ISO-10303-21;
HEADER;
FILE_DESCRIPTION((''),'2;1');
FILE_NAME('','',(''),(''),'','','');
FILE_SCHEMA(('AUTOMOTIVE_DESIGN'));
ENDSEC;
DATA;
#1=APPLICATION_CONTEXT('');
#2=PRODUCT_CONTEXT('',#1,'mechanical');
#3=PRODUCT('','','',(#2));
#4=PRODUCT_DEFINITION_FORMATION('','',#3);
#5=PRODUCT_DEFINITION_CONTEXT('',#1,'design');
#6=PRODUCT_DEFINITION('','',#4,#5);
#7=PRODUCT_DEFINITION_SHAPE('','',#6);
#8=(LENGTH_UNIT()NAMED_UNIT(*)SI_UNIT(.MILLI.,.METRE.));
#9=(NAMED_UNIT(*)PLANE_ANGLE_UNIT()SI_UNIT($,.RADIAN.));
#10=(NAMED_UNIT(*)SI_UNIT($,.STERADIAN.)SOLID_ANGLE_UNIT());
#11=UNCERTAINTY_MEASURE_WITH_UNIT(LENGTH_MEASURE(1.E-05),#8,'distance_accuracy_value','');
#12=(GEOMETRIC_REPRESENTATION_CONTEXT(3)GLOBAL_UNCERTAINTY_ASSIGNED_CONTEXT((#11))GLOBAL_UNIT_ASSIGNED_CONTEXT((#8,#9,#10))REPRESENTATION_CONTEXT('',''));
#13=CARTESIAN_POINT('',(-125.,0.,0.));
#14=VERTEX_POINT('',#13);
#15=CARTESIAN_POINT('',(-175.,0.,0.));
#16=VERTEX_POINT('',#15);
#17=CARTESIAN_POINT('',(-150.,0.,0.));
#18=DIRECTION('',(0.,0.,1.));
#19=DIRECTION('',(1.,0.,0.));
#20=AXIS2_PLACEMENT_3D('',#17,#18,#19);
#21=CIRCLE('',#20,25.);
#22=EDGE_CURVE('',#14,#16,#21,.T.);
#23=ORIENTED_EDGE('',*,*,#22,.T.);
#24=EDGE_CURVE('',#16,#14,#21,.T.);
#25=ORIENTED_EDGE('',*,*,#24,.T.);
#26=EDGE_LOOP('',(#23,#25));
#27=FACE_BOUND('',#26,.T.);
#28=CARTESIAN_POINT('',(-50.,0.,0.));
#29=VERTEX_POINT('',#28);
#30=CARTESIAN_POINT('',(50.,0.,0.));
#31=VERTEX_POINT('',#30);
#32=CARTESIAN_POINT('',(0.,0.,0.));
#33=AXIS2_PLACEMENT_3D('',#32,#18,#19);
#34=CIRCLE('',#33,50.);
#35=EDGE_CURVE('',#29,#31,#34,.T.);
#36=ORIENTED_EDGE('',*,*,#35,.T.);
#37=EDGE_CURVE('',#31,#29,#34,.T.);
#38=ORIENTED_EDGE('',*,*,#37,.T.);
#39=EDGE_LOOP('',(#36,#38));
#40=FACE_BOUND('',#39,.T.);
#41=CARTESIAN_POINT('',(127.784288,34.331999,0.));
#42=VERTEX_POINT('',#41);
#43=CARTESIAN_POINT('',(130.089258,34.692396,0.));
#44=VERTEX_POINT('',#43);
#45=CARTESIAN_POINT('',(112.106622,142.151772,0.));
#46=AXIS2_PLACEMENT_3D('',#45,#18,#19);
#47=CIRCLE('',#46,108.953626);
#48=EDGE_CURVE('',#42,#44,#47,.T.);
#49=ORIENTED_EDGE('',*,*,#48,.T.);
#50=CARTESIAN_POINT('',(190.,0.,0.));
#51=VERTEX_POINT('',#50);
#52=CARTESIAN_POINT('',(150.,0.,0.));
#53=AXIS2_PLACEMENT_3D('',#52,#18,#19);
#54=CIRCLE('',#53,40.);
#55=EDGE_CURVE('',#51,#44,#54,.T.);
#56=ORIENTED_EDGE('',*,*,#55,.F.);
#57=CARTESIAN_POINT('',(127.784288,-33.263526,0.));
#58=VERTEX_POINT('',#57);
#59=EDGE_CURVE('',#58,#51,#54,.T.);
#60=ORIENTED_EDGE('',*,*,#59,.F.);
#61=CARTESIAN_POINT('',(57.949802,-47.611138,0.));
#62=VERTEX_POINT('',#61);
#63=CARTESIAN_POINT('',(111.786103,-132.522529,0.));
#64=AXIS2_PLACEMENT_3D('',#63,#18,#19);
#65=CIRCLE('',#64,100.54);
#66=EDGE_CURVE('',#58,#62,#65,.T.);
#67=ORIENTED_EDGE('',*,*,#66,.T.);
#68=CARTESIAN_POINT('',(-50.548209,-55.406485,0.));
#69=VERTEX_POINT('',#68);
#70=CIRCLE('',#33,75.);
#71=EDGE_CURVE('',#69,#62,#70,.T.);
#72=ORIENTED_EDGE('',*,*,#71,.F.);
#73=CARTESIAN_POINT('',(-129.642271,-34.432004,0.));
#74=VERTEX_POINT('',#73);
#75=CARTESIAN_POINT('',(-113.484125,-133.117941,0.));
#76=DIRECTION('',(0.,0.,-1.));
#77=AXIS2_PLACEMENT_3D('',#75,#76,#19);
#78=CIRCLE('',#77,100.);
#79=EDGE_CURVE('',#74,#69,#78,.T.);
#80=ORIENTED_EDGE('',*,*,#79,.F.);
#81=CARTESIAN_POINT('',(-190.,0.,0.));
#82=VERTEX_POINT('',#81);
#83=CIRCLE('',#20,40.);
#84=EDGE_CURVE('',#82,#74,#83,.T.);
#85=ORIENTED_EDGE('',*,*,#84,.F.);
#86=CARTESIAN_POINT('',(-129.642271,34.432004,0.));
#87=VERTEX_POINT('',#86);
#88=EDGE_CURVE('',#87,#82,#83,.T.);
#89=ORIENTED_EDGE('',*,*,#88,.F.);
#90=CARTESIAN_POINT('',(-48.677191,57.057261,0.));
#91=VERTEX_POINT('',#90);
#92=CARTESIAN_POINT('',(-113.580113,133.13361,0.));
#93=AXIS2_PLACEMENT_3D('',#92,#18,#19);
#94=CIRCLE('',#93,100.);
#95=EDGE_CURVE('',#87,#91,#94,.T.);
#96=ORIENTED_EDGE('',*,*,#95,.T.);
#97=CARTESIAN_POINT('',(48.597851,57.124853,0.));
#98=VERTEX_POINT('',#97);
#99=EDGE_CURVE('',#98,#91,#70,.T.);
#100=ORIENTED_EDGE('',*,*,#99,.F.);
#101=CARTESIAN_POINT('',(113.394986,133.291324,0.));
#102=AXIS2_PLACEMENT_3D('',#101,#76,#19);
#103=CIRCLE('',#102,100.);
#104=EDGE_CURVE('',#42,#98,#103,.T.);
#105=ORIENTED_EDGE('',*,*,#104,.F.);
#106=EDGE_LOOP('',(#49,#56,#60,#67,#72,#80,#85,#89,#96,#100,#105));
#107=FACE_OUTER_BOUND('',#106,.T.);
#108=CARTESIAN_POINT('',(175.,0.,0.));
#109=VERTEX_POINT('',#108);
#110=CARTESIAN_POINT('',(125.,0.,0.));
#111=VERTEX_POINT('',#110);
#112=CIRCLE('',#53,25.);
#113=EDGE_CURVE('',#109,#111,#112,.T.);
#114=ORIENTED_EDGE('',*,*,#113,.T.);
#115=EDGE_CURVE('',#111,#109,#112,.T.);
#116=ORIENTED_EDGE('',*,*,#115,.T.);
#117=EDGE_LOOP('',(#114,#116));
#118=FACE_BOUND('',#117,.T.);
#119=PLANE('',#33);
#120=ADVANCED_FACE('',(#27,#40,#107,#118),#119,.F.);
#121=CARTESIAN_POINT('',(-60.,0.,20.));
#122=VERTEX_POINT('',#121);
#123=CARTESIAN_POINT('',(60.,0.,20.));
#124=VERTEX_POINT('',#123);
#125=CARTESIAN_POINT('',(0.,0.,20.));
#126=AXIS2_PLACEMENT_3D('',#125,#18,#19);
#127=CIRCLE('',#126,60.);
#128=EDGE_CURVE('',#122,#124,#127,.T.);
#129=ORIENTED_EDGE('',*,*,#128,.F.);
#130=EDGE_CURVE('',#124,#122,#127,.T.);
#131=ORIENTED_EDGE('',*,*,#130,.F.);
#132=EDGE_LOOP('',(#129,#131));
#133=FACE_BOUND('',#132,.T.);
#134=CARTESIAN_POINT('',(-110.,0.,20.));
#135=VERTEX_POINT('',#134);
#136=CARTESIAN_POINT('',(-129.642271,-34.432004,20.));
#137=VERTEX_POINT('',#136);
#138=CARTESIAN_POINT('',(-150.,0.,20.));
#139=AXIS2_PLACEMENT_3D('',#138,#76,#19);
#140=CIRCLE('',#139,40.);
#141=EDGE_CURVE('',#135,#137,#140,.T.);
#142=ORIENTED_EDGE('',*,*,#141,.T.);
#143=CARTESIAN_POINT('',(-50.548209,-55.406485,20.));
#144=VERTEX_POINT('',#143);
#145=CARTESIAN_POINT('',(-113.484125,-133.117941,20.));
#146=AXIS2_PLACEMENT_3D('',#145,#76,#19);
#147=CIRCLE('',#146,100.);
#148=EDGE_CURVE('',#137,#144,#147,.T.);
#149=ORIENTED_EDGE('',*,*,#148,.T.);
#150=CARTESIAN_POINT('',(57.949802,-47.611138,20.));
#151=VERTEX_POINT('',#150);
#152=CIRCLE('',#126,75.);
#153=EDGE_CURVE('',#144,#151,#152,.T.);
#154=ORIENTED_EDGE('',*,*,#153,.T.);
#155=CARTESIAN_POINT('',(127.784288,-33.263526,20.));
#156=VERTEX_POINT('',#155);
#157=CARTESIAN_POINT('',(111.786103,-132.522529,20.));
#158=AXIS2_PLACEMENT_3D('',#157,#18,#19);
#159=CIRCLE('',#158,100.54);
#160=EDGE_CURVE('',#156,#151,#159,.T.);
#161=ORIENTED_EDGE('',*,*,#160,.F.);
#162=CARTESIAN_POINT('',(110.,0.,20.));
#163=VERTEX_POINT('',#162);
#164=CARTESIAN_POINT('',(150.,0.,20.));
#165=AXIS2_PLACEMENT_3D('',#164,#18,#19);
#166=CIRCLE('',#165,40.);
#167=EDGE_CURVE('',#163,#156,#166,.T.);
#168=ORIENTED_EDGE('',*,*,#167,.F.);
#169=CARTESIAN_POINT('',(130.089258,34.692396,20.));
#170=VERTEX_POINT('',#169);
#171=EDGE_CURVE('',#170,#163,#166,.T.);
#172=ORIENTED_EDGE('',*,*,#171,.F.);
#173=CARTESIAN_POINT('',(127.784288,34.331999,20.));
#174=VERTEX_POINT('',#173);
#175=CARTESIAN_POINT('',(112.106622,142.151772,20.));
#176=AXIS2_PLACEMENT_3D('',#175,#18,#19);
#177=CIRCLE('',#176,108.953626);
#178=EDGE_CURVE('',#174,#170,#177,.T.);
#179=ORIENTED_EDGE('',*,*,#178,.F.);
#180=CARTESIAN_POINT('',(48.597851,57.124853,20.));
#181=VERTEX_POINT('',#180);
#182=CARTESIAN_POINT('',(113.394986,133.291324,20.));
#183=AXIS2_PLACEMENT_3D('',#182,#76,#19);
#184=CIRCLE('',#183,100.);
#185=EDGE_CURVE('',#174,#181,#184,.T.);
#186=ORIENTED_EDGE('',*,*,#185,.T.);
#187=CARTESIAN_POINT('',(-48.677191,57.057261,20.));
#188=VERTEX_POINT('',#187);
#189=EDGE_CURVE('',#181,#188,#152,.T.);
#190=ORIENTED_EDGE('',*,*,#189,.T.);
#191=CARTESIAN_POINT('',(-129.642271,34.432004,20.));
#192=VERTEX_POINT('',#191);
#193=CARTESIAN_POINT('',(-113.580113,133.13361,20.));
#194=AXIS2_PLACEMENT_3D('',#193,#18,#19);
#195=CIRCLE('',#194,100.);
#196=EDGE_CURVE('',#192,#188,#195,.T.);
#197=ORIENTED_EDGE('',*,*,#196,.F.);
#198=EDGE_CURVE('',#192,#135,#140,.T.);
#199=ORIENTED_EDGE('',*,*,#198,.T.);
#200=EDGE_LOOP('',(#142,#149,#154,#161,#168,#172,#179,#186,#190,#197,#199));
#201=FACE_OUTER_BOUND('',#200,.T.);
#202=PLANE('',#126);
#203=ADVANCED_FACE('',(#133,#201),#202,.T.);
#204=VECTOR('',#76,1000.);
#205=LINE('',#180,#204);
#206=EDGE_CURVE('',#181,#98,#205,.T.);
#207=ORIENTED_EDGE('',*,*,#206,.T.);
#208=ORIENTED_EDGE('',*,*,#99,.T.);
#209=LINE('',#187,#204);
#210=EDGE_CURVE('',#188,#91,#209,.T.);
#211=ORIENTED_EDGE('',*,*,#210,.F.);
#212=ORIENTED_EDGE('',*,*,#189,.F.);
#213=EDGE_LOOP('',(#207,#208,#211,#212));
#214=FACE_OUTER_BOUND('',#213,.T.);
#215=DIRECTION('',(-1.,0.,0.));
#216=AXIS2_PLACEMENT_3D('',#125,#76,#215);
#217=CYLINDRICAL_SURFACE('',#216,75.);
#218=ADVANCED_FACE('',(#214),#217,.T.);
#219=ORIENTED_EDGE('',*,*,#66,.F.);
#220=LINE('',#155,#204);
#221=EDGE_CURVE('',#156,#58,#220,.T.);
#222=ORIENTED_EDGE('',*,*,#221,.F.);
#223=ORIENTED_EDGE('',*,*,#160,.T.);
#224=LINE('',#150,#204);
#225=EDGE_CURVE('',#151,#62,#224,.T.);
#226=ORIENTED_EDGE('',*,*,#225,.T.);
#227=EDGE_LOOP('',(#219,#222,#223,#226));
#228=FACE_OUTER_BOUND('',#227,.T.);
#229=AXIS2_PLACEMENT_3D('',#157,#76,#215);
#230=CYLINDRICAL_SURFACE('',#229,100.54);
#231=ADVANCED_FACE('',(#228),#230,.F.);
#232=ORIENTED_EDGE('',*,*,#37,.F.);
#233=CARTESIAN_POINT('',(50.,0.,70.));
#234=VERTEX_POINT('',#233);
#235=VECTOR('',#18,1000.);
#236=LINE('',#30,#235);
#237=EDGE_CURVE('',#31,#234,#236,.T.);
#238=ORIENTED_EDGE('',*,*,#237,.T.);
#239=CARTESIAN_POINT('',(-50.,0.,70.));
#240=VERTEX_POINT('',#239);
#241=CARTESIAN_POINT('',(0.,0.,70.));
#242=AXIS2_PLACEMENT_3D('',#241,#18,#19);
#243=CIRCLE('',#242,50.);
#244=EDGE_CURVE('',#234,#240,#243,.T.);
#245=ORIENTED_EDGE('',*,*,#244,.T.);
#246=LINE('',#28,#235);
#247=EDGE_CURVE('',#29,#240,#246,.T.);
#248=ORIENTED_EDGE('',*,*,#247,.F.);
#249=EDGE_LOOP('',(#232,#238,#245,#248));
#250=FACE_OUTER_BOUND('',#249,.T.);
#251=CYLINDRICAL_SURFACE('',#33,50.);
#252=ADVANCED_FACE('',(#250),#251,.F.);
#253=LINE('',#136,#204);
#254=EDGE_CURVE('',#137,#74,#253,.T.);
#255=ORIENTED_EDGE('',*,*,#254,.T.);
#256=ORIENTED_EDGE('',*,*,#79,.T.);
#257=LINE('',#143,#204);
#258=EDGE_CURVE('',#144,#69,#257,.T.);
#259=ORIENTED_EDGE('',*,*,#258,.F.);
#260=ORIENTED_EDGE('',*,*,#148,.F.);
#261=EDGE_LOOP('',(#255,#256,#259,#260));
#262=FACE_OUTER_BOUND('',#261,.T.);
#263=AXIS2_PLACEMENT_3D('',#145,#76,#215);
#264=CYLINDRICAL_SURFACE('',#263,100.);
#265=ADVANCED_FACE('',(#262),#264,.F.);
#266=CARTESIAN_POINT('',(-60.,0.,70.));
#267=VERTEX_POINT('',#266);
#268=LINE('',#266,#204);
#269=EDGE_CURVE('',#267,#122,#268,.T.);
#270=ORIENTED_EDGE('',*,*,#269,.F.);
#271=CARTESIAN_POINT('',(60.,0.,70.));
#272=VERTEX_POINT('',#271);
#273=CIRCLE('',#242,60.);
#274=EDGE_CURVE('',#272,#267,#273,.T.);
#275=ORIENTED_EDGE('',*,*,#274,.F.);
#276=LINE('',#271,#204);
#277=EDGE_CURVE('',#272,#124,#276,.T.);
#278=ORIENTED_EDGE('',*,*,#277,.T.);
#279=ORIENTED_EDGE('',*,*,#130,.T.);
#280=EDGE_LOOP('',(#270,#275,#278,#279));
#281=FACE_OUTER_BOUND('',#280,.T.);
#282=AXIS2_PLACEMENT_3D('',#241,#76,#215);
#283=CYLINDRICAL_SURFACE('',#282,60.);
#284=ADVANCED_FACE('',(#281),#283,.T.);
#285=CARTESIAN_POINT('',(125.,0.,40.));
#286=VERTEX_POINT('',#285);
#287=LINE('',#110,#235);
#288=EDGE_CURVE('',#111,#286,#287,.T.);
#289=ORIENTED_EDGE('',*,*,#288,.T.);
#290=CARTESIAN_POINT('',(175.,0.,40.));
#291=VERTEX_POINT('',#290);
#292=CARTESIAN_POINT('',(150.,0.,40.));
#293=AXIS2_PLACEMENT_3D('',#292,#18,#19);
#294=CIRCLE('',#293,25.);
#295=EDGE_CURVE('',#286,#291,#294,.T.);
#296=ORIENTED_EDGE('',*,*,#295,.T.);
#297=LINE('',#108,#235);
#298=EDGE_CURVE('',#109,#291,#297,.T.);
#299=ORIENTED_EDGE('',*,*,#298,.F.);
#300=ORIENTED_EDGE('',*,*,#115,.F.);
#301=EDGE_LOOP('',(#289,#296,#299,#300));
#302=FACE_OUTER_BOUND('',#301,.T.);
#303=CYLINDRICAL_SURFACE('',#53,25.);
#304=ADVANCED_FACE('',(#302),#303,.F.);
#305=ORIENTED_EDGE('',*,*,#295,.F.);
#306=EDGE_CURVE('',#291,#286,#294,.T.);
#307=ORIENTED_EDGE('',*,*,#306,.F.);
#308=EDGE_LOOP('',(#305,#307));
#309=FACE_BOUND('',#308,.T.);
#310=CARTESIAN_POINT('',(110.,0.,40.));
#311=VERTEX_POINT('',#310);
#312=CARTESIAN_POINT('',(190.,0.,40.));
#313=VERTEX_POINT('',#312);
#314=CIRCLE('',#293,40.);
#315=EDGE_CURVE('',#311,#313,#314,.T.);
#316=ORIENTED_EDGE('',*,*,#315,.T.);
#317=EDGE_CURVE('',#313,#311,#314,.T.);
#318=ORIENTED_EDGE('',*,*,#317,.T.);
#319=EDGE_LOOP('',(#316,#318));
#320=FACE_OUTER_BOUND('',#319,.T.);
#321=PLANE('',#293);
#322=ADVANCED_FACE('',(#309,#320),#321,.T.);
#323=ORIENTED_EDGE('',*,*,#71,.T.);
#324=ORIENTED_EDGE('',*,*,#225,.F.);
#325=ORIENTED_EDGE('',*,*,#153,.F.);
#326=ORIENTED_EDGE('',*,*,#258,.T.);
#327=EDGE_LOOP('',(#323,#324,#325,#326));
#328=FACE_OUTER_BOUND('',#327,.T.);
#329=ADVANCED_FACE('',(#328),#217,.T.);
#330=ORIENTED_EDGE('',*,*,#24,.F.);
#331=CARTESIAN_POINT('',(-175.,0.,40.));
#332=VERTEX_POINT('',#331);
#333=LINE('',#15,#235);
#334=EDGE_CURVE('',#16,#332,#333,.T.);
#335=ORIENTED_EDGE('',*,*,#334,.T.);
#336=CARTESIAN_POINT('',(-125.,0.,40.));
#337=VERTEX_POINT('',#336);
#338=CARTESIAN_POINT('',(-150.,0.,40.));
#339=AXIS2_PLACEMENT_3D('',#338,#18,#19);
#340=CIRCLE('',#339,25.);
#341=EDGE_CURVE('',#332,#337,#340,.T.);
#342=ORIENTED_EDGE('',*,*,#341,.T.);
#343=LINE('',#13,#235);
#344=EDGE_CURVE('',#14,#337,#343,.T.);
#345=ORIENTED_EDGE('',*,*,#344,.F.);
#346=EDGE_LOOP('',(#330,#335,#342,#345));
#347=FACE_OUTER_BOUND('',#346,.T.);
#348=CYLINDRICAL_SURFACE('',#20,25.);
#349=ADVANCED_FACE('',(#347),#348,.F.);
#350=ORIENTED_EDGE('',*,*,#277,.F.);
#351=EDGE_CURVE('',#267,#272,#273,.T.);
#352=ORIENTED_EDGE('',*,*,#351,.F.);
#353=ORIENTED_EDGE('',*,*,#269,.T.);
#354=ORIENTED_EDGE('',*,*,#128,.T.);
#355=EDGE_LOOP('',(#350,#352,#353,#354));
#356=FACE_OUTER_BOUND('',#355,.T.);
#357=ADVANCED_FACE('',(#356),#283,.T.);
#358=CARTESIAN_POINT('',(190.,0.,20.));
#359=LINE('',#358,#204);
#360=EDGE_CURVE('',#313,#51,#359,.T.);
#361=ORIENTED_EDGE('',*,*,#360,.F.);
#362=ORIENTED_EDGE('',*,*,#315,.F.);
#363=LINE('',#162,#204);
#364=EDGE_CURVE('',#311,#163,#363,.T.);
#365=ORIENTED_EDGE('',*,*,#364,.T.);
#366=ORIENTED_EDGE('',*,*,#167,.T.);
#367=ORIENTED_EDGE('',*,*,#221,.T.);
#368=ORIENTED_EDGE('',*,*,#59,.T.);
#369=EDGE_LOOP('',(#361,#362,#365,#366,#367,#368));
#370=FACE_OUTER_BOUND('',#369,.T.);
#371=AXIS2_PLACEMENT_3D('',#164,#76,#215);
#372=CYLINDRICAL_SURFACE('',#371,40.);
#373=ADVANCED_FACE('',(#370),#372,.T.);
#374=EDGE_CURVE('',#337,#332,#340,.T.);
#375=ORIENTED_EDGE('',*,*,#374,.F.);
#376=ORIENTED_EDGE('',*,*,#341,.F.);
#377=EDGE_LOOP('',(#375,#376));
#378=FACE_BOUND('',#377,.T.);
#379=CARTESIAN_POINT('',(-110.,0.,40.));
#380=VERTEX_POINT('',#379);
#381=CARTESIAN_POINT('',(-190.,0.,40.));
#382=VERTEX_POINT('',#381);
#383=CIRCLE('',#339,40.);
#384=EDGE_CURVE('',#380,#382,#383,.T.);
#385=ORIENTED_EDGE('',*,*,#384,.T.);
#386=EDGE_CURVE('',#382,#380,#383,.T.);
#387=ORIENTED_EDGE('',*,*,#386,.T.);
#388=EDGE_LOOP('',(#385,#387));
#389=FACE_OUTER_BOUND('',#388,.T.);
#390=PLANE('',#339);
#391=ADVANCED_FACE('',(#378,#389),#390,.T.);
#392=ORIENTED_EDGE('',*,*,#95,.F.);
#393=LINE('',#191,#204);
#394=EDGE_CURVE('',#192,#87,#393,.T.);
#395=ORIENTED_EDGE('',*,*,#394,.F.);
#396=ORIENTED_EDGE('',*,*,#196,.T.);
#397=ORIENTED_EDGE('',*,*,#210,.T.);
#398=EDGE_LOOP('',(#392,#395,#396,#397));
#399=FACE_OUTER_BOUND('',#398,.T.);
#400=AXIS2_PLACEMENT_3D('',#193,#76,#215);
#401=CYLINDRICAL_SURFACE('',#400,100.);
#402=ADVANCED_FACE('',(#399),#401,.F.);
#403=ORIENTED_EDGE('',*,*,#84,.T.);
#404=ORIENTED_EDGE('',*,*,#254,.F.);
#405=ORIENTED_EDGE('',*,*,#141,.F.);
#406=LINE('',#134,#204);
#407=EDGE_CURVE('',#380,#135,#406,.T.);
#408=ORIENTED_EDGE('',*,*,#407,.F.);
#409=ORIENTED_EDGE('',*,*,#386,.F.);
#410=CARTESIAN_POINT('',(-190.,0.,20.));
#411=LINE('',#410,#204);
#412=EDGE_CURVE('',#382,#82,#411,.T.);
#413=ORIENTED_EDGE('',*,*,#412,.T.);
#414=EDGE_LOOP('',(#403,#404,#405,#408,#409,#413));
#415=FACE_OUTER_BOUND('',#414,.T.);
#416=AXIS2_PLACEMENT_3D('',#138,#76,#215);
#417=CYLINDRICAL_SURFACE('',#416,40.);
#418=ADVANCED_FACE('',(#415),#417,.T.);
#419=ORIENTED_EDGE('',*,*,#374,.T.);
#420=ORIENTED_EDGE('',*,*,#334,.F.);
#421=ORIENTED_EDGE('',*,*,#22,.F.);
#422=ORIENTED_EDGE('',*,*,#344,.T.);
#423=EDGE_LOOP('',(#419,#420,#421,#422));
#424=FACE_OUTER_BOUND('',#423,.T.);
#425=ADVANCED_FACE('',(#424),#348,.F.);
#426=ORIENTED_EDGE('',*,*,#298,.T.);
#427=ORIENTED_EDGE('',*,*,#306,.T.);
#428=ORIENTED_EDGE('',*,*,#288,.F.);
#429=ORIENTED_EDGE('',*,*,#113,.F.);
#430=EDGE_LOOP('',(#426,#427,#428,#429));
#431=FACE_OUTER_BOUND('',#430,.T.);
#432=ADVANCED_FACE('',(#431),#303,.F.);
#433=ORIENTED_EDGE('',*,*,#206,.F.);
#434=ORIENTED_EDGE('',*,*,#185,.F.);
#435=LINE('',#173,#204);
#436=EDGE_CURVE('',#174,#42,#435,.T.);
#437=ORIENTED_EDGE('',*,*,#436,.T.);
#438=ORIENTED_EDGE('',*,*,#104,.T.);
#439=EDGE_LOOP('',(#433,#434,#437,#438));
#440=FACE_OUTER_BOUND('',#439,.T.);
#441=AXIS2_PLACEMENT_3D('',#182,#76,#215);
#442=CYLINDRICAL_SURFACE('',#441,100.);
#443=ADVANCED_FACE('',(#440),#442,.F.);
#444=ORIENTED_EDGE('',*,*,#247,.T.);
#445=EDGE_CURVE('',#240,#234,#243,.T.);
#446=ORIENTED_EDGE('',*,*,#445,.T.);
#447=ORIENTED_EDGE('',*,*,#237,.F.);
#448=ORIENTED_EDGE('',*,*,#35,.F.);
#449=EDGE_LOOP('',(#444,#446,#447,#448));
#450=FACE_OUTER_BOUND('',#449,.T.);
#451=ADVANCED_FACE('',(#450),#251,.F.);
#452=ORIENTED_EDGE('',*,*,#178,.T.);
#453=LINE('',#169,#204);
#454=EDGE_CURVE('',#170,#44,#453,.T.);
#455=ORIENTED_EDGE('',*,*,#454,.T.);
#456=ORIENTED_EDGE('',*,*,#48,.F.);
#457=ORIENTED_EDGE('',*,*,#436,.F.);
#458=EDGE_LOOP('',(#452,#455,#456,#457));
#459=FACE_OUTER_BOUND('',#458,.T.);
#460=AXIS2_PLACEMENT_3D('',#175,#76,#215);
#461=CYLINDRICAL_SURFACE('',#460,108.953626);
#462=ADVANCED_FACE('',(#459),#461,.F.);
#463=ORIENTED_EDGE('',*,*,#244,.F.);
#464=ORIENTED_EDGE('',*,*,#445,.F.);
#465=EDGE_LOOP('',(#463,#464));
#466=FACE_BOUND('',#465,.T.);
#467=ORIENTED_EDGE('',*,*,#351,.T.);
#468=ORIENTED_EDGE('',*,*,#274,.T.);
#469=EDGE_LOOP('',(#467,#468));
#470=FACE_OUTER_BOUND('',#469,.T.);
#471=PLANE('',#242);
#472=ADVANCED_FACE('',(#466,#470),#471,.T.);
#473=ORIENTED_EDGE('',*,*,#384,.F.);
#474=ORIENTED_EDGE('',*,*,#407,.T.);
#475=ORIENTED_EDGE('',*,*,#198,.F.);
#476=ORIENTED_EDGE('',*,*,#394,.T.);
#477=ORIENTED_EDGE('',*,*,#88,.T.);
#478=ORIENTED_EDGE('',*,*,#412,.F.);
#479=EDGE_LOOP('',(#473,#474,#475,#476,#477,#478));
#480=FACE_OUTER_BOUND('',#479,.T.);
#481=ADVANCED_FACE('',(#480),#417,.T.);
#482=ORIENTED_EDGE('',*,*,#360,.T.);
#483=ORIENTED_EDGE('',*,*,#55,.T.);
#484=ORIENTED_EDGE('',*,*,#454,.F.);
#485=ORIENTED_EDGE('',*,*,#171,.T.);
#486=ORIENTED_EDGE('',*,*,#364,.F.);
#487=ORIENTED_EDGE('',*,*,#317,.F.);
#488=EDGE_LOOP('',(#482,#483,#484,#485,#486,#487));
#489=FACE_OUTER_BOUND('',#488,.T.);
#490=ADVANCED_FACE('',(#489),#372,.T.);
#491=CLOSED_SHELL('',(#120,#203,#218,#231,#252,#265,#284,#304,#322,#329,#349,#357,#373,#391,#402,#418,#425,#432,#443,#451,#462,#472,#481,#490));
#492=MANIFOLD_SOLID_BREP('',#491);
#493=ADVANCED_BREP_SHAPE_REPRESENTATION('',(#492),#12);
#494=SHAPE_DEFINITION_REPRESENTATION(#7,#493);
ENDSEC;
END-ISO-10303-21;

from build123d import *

# Parameters (mm, degrees)
LINK_PLATE_DEPTH      = 20
CENTER_BOSS_SKETCH_R  = 60
CENTER_BOSS_120_DEPTH = 50
CENTER_BORE_SKETCH_R  = 50
CENTER_BORE_100_DEPTH = 70
END_BOSS_A_SKETCH_R   = 40
END_BOSS_A_80_DEPTH   = 20
END_BOSS_B_SKETCH_R   = 40
END_BOSS_B_80_DEPTH   = 20
END_BORES_SKETCH_R    = 25
END_BORES_2X_50_DEPTH = 40


with BuildPart() as part:
    # Link Profile Sketch → Link Plate (new body)
    with BuildSketch(Plane.XY):
        with BuildLine():
            ThreePointArc((-129.642270948, 34.432003541), (-190, 0), (-129.642270948, -34.432003541))
            ThreePointArc((-129.642270948, -34.432003541), (-87.851681721, -36.458860817), (-50.548209333, -55.406484578))
            ThreePointArc((-50.548209333, -55.406484578), (5.374732367, -74.807167116), (57.949801632, -47.611138306))
            ThreePointArc((57.949801632, -47.611138306), (91.552609541, -34.039548838), (127.784288058, -33.263525714))
            ThreePointArc((127.784288058, -33.263525714), (189.977010396, -1.355964531), (130.089258317, 34.692396366))
            ThreePointArc((130.089258317, 34.692396366), (128.937737844, 34.506028192), (127.784288058, 34.331999196))
            ThreePointArc((127.784288058, 34.331999196), (85.734256685, 37.193020101), (48.597851254, 57.124853204))
            ThreePointArc((48.597851254, 57.124853204), (-0.052113987, 74.999981894), (-48.677191075, 57.057261317))
            ThreePointArc((-48.677191075, 57.057261317), (-86.6667217, 36.823333055), (-129.642270948, 34.432003541))
        make_face()
    extrude(amount=LINK_PLATE_DEPTH)

    # Center Boss Sketch → Center Boss Ø120 (add)
    with BuildSketch(Plane.XY.offset(20)):
        Circle(CENTER_BOSS_SKETCH_R)
    extrude(amount=CENTER_BOSS_120_DEPTH)

    # Center Bore Sketch → Center Bore Ø100 (cut)
    with BuildSketch(Plane.XY.offset(70)):
        Circle(CENTER_BORE_SKETCH_R)
    extrude(amount=-CENTER_BORE_100_DEPTH, mode=Mode.SUBTRACT)

    # End Boss A Sketch → End Boss A Ø80 (add)
    with BuildSketch(Plane.XY.offset(20)):
        with Locations(Location((-150, 0, 0), (0, 0, 300.593464185))):
            Circle(END_BOSS_A_SKETCH_R)
    extrude(amount=END_BOSS_A_80_DEPTH)

    # End Boss B Sketch → End Boss B Ø80 (add)
    with BuildSketch(Plane.XY.offset(20)):
        with Locations(Location((150, 0, 0), (0, 0, 236.26222597))):
            Circle(END_BOSS_B_SKETCH_R)
    extrude(amount=END_BOSS_B_80_DEPTH)

    # End Bores Sketch → End Bores 2xØ50 (cut)
    with BuildSketch(Plane.XY.offset(40)):
        with Locations((-150, 0)):
            Circle(END_BORES_SKETCH_R)
        with Locations((150, 0)):
            Circle(END_BORES_SKETCH_R)
    extrude(amount=-END_BORES_2X_50_DEPTH, mode=Mode.SUBTRACT)


solid = part.part
